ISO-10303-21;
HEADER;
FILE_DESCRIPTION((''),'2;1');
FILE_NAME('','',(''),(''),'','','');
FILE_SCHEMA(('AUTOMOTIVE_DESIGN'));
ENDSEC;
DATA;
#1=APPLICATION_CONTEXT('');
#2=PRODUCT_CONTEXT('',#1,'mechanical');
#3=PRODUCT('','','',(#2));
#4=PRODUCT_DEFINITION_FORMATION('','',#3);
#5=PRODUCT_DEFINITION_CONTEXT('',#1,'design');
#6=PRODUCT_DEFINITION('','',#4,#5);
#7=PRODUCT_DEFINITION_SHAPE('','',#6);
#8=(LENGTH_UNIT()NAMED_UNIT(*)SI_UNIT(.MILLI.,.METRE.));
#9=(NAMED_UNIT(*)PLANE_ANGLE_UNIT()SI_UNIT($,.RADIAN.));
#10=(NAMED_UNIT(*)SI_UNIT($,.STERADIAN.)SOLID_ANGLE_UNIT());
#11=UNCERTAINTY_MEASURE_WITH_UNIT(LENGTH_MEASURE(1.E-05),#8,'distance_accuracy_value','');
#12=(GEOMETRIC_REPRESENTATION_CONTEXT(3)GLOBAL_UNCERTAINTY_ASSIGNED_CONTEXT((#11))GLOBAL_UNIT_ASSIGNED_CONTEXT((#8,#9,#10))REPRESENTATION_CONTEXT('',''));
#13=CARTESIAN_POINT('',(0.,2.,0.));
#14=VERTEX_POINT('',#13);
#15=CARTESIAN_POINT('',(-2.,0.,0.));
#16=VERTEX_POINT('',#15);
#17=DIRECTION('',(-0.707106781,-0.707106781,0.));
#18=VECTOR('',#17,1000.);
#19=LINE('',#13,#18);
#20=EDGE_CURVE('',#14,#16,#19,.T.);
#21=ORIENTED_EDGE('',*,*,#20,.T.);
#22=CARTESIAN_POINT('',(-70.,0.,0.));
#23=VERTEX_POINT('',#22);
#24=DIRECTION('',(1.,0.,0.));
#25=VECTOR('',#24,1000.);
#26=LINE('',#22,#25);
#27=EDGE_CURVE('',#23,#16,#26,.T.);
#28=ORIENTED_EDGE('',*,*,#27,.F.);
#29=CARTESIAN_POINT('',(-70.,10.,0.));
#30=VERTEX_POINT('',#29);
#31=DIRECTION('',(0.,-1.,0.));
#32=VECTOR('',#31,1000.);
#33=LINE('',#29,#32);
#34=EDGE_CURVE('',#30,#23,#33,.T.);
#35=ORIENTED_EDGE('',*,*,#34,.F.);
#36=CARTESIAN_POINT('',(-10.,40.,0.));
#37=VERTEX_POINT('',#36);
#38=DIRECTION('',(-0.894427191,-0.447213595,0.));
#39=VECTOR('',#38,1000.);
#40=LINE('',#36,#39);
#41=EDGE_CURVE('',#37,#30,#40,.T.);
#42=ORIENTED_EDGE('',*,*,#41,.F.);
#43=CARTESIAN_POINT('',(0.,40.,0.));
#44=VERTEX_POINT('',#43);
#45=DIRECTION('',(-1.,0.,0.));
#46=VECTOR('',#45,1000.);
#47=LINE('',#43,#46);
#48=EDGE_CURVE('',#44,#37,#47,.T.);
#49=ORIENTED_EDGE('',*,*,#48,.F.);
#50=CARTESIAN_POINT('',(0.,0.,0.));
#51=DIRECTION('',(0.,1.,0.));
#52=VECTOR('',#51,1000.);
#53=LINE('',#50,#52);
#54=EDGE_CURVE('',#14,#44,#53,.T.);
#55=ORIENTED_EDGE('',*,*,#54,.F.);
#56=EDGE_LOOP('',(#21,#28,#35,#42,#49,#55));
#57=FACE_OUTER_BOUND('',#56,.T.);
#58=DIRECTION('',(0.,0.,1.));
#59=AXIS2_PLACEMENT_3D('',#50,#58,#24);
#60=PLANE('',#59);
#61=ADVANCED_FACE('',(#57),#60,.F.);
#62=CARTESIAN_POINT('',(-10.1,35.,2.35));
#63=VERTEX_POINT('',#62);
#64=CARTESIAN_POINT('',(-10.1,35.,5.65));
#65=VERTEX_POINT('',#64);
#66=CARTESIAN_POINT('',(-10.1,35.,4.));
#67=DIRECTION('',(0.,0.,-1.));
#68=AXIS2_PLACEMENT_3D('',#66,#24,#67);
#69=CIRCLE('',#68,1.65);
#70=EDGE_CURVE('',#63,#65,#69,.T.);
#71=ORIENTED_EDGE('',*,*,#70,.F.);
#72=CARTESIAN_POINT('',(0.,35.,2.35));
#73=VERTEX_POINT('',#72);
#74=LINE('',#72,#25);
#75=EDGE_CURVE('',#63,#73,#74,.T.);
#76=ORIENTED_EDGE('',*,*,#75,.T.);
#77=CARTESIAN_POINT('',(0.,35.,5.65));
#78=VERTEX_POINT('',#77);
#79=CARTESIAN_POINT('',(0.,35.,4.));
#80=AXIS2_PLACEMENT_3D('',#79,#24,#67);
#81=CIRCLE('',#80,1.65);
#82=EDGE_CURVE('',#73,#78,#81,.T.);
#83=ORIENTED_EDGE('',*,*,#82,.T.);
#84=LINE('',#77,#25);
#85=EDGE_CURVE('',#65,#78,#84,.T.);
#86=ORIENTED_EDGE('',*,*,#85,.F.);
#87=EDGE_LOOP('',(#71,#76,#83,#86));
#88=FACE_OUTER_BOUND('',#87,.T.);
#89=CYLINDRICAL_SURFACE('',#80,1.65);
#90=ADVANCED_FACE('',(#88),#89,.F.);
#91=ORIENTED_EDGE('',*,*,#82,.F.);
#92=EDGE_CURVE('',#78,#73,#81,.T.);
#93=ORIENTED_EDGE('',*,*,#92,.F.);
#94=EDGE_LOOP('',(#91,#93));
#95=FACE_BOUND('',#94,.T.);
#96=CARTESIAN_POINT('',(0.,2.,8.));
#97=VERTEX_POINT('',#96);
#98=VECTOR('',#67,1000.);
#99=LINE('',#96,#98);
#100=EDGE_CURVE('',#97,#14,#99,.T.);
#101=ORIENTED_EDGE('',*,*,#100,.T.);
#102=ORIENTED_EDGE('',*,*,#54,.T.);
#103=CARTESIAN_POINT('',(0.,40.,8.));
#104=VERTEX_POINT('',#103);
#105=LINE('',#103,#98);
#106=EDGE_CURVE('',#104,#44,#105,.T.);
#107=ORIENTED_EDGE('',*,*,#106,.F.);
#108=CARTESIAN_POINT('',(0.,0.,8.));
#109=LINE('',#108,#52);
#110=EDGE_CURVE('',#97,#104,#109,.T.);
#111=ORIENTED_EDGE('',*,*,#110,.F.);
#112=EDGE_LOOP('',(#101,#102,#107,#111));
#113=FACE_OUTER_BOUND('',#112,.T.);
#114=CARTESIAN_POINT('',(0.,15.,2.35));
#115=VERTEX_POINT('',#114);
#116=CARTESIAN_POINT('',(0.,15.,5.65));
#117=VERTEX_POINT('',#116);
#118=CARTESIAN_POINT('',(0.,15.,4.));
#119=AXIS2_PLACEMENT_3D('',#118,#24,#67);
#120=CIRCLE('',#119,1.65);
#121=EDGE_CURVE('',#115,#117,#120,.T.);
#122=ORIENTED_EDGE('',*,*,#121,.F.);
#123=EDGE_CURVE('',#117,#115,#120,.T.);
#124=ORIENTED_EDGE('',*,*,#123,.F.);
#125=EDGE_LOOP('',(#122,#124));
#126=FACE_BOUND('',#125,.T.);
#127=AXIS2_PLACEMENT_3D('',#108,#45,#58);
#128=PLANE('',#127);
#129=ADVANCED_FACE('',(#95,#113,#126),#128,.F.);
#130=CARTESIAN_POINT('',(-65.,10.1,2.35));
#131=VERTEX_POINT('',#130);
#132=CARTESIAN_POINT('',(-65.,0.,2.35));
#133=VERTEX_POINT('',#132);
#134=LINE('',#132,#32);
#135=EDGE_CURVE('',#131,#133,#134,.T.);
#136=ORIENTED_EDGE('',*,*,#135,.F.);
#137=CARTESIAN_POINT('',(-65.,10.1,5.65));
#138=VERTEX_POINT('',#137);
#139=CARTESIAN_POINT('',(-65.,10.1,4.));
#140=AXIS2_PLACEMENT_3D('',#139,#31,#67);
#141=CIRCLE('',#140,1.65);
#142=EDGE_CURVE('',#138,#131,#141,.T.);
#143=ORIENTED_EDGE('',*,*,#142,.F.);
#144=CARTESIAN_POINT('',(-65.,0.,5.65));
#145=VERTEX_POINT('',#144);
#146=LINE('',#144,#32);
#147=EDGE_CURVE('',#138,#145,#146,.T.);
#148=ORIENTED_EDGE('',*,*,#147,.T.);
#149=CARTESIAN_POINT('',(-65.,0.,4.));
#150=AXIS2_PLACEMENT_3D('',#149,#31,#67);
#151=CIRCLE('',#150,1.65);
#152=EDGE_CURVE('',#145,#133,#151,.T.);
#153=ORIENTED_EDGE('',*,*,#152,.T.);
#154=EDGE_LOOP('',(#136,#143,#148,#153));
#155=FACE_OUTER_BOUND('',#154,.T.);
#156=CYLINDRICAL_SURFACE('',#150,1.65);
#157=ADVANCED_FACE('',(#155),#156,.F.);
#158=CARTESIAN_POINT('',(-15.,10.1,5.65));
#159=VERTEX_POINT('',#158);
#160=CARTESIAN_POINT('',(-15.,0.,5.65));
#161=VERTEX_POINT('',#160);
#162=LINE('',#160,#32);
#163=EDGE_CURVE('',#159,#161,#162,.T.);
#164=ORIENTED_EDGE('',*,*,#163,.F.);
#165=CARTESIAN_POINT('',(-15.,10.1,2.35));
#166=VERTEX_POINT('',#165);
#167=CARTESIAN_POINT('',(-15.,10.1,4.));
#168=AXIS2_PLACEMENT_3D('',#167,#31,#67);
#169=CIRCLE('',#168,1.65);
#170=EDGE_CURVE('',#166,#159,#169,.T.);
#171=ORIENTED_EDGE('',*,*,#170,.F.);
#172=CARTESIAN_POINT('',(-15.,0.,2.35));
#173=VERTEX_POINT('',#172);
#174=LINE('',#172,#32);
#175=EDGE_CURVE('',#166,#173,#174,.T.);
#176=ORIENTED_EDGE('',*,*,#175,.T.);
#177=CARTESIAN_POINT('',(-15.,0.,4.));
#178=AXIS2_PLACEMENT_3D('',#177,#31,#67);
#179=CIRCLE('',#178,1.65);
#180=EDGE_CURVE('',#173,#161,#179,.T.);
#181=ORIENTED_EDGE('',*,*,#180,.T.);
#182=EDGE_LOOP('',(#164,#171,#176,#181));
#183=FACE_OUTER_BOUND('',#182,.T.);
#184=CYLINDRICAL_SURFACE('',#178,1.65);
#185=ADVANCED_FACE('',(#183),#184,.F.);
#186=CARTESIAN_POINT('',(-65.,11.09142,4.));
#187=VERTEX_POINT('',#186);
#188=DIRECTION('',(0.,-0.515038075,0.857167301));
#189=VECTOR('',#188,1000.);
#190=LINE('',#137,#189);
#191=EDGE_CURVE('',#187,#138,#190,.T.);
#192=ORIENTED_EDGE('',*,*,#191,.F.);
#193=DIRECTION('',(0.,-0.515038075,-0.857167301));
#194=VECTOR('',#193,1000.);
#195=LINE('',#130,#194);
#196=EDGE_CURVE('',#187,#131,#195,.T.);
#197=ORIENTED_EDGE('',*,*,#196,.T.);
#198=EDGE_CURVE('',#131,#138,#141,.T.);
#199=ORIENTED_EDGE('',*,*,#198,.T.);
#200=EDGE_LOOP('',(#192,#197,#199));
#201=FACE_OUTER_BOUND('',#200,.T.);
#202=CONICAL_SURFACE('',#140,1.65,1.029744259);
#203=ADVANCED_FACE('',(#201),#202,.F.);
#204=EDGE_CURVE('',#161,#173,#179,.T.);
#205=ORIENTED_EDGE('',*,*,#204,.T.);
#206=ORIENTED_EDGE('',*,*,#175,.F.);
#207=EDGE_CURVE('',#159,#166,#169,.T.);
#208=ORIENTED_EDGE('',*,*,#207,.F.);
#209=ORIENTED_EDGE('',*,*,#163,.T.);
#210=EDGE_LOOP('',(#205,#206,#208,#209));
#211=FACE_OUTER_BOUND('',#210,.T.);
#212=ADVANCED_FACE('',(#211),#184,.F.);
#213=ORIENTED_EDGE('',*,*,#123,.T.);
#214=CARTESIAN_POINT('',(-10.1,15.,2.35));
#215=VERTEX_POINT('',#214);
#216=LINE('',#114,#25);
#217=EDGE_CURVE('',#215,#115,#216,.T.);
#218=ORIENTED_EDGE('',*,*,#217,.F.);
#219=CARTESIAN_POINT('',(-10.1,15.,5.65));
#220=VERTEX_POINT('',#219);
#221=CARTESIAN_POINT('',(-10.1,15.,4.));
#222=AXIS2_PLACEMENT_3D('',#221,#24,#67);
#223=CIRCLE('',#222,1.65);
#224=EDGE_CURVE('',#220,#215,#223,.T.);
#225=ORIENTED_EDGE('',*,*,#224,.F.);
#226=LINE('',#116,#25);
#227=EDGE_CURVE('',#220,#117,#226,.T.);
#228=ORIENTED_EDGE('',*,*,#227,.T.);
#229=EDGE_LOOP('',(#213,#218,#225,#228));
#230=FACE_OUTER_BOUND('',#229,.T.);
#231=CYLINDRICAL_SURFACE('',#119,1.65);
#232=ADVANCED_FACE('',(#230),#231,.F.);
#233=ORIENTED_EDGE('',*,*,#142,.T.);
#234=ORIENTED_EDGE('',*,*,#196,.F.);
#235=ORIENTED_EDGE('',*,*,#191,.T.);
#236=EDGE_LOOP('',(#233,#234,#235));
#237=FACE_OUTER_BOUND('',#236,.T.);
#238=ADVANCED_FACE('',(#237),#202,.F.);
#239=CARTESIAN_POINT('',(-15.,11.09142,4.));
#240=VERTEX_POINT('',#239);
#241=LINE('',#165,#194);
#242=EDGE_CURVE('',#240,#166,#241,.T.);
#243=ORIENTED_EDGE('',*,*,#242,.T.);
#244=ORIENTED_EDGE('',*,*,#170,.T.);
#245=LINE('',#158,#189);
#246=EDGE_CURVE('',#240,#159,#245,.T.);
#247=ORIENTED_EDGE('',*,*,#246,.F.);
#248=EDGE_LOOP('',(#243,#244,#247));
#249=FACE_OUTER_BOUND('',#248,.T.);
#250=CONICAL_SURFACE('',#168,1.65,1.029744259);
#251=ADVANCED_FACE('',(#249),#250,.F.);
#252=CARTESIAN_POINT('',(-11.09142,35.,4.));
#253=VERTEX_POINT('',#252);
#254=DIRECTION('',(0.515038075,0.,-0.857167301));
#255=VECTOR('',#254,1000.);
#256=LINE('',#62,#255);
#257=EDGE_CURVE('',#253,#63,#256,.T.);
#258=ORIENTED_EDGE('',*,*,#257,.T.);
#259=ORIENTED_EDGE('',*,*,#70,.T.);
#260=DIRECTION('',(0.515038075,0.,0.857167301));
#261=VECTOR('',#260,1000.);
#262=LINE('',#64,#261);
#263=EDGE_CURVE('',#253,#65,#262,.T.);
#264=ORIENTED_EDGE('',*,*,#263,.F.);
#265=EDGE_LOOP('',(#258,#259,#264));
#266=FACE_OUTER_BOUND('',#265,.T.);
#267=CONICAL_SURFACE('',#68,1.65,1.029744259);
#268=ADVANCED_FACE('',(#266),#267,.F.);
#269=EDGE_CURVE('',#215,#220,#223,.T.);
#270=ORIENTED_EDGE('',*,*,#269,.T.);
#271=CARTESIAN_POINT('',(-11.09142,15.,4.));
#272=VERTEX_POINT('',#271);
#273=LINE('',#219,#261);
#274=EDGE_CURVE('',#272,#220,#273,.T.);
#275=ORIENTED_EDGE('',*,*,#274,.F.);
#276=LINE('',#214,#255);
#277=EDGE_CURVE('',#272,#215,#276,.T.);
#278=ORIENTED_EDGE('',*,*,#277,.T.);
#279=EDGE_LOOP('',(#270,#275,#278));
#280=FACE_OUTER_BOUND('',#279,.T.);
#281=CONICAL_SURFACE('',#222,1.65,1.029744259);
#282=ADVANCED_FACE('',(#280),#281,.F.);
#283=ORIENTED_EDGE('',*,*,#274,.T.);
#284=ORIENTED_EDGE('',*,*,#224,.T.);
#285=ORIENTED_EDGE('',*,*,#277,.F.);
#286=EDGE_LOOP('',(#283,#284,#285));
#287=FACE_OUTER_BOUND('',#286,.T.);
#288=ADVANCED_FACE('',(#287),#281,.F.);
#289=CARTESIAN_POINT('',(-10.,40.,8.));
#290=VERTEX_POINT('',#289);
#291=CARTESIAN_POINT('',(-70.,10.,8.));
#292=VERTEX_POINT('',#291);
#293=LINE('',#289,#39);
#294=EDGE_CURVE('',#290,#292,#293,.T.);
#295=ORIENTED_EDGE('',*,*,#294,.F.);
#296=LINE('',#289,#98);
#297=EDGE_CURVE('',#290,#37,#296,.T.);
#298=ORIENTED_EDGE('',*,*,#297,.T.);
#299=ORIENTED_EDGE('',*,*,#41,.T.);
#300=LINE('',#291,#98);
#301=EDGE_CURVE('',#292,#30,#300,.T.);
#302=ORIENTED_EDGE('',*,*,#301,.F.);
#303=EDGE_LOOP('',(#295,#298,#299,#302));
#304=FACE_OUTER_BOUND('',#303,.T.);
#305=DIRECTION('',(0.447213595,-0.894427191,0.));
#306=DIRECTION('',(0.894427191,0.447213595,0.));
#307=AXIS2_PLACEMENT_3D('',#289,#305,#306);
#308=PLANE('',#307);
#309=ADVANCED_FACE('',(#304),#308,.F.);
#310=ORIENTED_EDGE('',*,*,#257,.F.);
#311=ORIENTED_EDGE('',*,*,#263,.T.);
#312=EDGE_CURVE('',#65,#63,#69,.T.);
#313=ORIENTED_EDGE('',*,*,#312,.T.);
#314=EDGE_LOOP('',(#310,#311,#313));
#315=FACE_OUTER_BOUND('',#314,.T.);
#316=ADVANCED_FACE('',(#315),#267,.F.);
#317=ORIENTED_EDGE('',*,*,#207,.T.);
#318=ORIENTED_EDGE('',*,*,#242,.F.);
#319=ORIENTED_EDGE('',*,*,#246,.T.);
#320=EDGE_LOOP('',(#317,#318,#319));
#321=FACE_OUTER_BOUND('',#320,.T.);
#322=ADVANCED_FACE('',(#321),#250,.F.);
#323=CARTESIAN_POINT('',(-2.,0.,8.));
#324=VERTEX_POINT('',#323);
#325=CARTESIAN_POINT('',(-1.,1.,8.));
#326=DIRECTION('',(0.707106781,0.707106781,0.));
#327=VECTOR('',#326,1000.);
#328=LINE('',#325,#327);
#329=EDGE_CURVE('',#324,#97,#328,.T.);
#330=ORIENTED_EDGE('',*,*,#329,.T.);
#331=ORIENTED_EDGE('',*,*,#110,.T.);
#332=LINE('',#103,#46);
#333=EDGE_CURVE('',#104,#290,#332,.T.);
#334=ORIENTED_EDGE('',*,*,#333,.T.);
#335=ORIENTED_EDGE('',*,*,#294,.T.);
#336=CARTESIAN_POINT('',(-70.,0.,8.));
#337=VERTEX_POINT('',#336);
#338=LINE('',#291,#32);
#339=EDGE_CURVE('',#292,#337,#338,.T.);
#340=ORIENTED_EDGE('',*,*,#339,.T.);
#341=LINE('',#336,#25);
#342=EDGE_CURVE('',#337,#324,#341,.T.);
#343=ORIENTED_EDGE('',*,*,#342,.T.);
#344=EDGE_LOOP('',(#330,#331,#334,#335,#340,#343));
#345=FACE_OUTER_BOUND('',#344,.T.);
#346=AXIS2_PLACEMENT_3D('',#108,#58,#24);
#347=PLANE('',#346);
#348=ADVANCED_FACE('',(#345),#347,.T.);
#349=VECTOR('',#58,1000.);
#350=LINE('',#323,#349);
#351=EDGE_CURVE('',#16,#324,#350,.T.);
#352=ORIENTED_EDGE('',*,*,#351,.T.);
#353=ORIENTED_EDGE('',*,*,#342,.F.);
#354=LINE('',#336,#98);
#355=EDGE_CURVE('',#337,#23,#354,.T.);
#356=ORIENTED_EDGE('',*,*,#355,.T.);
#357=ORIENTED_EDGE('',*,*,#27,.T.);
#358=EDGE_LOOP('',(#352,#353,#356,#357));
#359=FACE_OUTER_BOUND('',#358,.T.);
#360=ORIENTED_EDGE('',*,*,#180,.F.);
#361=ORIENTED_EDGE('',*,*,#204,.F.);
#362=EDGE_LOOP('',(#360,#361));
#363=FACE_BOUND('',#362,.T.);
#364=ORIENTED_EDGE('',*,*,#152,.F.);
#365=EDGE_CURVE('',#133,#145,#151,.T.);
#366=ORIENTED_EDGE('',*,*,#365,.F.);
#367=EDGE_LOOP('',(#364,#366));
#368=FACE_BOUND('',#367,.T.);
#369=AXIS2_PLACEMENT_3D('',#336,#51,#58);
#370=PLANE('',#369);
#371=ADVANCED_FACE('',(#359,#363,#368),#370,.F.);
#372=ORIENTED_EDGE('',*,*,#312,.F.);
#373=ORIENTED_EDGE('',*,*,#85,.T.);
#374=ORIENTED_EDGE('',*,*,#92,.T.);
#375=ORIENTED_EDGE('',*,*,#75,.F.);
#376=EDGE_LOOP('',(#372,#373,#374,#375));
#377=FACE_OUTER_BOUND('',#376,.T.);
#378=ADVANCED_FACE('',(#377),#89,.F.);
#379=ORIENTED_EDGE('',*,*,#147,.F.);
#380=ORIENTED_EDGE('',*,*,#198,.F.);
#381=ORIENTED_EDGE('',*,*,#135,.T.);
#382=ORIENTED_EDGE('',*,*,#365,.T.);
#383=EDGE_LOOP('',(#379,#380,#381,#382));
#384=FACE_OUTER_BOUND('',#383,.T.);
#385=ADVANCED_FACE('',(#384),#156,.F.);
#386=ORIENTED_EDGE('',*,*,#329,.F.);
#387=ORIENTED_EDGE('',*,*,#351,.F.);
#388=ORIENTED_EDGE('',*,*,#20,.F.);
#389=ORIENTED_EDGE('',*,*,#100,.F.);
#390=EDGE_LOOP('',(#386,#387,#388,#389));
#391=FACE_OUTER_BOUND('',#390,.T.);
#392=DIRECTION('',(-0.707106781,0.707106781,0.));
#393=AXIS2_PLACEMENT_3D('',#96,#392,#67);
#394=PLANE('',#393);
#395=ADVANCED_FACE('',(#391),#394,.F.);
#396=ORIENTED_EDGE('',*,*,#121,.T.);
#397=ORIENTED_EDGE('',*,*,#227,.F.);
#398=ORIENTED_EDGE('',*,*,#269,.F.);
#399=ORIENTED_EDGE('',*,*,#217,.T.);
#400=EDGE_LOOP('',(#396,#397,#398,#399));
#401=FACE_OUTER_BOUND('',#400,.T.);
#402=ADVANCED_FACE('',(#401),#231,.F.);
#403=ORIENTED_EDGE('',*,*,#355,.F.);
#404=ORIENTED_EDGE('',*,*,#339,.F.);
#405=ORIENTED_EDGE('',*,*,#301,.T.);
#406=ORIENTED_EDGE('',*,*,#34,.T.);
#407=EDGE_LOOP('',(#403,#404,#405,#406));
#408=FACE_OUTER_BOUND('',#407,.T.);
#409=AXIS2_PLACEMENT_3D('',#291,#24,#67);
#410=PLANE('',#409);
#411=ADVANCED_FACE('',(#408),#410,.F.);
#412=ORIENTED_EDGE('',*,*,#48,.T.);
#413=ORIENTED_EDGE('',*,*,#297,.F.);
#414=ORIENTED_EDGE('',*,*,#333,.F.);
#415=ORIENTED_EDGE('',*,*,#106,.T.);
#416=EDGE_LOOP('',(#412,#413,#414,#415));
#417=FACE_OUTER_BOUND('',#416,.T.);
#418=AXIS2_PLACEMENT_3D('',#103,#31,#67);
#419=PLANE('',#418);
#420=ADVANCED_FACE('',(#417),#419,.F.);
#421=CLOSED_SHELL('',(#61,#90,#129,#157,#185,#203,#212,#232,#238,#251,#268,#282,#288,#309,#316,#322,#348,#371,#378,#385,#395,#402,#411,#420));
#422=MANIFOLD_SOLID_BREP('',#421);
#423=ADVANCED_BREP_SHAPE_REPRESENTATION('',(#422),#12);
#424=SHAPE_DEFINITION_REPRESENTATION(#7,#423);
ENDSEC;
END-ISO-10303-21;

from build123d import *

# Parameters (mm, degrees)
EXTRUDE_1_DEPTH        = 8
HOLE_WIZARD_M4_2_D     = 3.3
HOLE_WIZARD_M4_2_DEPTH = 10.1
HOLE_WIZARD_M4_2_TIP   = 0.991420021
HOLE_WIZARD_M4_1_D     = 3.3
HOLE_WIZARD_M4_1_DEPTH = 10.1
HOLE_WIZARD_M4_1_TIP   = 0.991420021
CHAMFER_1_SIZE         = 2


with BuildPart() as part:
    # 草图1 → 凸台-拉伸1 (new body)
    with BuildSketch(Plane.XY):
        Polygon((0, 0), (0, 40), (-10, 40), (-70, 10), (-70, 0), align=None)
    extrude(amount=EXTRUDE_1_DEPTH)

    # M4 螺纹孔2
    with Locations(Plane(origin=(0, 0, 0), x_dir=(-1, 0, 0), z_dir=(0, -1, 0))):
        with Locations((15, -4), (65, -4)):
            Hole(HOLE_WIZARD_M4_2_D / 2, depth=HOLE_WIZARD_M4_2_DEPTH)
            with Locations((0, 0, -(HOLE_WIZARD_M4_2_DEPTH + HOLE_WIZARD_M4_2_TIP / 2))):  # 118° drill point
                Cone(0, HOLE_WIZARD_M4_2_D / 2, HOLE_WIZARD_M4_2_TIP, mode=Mode.SUBTRACT)

    # M4 螺纹孔1
    with Locations(Plane(origin=(0, 0, 0), x_dir=(0, 0, -1), z_dir=(1, 0, 0))):
        with Locations((-4, 35), (-4, 15)):
            Hole(HOLE_WIZARD_M4_1_D / 2, depth=HOLE_WIZARD_M4_1_DEPTH)
            with Locations((0, 0, -(HOLE_WIZARD_M4_1_DEPTH + HOLE_WIZARD_M4_1_TIP / 2))):  # 118° drill point
                Cone(0, HOLE_WIZARD_M4_1_D / 2, HOLE_WIZARD_M4_1_TIP, mode=Mode.SUBTRACT)

    # 倒角1
    chamfer_1_edges = [part.edges().sort_by_distance(p)[0] for p in [
        (0, 0, 4),
    ]]
    chamfer(chamfer_1_edges, length=CHAMFER_1_SIZE)


solid = part.part
